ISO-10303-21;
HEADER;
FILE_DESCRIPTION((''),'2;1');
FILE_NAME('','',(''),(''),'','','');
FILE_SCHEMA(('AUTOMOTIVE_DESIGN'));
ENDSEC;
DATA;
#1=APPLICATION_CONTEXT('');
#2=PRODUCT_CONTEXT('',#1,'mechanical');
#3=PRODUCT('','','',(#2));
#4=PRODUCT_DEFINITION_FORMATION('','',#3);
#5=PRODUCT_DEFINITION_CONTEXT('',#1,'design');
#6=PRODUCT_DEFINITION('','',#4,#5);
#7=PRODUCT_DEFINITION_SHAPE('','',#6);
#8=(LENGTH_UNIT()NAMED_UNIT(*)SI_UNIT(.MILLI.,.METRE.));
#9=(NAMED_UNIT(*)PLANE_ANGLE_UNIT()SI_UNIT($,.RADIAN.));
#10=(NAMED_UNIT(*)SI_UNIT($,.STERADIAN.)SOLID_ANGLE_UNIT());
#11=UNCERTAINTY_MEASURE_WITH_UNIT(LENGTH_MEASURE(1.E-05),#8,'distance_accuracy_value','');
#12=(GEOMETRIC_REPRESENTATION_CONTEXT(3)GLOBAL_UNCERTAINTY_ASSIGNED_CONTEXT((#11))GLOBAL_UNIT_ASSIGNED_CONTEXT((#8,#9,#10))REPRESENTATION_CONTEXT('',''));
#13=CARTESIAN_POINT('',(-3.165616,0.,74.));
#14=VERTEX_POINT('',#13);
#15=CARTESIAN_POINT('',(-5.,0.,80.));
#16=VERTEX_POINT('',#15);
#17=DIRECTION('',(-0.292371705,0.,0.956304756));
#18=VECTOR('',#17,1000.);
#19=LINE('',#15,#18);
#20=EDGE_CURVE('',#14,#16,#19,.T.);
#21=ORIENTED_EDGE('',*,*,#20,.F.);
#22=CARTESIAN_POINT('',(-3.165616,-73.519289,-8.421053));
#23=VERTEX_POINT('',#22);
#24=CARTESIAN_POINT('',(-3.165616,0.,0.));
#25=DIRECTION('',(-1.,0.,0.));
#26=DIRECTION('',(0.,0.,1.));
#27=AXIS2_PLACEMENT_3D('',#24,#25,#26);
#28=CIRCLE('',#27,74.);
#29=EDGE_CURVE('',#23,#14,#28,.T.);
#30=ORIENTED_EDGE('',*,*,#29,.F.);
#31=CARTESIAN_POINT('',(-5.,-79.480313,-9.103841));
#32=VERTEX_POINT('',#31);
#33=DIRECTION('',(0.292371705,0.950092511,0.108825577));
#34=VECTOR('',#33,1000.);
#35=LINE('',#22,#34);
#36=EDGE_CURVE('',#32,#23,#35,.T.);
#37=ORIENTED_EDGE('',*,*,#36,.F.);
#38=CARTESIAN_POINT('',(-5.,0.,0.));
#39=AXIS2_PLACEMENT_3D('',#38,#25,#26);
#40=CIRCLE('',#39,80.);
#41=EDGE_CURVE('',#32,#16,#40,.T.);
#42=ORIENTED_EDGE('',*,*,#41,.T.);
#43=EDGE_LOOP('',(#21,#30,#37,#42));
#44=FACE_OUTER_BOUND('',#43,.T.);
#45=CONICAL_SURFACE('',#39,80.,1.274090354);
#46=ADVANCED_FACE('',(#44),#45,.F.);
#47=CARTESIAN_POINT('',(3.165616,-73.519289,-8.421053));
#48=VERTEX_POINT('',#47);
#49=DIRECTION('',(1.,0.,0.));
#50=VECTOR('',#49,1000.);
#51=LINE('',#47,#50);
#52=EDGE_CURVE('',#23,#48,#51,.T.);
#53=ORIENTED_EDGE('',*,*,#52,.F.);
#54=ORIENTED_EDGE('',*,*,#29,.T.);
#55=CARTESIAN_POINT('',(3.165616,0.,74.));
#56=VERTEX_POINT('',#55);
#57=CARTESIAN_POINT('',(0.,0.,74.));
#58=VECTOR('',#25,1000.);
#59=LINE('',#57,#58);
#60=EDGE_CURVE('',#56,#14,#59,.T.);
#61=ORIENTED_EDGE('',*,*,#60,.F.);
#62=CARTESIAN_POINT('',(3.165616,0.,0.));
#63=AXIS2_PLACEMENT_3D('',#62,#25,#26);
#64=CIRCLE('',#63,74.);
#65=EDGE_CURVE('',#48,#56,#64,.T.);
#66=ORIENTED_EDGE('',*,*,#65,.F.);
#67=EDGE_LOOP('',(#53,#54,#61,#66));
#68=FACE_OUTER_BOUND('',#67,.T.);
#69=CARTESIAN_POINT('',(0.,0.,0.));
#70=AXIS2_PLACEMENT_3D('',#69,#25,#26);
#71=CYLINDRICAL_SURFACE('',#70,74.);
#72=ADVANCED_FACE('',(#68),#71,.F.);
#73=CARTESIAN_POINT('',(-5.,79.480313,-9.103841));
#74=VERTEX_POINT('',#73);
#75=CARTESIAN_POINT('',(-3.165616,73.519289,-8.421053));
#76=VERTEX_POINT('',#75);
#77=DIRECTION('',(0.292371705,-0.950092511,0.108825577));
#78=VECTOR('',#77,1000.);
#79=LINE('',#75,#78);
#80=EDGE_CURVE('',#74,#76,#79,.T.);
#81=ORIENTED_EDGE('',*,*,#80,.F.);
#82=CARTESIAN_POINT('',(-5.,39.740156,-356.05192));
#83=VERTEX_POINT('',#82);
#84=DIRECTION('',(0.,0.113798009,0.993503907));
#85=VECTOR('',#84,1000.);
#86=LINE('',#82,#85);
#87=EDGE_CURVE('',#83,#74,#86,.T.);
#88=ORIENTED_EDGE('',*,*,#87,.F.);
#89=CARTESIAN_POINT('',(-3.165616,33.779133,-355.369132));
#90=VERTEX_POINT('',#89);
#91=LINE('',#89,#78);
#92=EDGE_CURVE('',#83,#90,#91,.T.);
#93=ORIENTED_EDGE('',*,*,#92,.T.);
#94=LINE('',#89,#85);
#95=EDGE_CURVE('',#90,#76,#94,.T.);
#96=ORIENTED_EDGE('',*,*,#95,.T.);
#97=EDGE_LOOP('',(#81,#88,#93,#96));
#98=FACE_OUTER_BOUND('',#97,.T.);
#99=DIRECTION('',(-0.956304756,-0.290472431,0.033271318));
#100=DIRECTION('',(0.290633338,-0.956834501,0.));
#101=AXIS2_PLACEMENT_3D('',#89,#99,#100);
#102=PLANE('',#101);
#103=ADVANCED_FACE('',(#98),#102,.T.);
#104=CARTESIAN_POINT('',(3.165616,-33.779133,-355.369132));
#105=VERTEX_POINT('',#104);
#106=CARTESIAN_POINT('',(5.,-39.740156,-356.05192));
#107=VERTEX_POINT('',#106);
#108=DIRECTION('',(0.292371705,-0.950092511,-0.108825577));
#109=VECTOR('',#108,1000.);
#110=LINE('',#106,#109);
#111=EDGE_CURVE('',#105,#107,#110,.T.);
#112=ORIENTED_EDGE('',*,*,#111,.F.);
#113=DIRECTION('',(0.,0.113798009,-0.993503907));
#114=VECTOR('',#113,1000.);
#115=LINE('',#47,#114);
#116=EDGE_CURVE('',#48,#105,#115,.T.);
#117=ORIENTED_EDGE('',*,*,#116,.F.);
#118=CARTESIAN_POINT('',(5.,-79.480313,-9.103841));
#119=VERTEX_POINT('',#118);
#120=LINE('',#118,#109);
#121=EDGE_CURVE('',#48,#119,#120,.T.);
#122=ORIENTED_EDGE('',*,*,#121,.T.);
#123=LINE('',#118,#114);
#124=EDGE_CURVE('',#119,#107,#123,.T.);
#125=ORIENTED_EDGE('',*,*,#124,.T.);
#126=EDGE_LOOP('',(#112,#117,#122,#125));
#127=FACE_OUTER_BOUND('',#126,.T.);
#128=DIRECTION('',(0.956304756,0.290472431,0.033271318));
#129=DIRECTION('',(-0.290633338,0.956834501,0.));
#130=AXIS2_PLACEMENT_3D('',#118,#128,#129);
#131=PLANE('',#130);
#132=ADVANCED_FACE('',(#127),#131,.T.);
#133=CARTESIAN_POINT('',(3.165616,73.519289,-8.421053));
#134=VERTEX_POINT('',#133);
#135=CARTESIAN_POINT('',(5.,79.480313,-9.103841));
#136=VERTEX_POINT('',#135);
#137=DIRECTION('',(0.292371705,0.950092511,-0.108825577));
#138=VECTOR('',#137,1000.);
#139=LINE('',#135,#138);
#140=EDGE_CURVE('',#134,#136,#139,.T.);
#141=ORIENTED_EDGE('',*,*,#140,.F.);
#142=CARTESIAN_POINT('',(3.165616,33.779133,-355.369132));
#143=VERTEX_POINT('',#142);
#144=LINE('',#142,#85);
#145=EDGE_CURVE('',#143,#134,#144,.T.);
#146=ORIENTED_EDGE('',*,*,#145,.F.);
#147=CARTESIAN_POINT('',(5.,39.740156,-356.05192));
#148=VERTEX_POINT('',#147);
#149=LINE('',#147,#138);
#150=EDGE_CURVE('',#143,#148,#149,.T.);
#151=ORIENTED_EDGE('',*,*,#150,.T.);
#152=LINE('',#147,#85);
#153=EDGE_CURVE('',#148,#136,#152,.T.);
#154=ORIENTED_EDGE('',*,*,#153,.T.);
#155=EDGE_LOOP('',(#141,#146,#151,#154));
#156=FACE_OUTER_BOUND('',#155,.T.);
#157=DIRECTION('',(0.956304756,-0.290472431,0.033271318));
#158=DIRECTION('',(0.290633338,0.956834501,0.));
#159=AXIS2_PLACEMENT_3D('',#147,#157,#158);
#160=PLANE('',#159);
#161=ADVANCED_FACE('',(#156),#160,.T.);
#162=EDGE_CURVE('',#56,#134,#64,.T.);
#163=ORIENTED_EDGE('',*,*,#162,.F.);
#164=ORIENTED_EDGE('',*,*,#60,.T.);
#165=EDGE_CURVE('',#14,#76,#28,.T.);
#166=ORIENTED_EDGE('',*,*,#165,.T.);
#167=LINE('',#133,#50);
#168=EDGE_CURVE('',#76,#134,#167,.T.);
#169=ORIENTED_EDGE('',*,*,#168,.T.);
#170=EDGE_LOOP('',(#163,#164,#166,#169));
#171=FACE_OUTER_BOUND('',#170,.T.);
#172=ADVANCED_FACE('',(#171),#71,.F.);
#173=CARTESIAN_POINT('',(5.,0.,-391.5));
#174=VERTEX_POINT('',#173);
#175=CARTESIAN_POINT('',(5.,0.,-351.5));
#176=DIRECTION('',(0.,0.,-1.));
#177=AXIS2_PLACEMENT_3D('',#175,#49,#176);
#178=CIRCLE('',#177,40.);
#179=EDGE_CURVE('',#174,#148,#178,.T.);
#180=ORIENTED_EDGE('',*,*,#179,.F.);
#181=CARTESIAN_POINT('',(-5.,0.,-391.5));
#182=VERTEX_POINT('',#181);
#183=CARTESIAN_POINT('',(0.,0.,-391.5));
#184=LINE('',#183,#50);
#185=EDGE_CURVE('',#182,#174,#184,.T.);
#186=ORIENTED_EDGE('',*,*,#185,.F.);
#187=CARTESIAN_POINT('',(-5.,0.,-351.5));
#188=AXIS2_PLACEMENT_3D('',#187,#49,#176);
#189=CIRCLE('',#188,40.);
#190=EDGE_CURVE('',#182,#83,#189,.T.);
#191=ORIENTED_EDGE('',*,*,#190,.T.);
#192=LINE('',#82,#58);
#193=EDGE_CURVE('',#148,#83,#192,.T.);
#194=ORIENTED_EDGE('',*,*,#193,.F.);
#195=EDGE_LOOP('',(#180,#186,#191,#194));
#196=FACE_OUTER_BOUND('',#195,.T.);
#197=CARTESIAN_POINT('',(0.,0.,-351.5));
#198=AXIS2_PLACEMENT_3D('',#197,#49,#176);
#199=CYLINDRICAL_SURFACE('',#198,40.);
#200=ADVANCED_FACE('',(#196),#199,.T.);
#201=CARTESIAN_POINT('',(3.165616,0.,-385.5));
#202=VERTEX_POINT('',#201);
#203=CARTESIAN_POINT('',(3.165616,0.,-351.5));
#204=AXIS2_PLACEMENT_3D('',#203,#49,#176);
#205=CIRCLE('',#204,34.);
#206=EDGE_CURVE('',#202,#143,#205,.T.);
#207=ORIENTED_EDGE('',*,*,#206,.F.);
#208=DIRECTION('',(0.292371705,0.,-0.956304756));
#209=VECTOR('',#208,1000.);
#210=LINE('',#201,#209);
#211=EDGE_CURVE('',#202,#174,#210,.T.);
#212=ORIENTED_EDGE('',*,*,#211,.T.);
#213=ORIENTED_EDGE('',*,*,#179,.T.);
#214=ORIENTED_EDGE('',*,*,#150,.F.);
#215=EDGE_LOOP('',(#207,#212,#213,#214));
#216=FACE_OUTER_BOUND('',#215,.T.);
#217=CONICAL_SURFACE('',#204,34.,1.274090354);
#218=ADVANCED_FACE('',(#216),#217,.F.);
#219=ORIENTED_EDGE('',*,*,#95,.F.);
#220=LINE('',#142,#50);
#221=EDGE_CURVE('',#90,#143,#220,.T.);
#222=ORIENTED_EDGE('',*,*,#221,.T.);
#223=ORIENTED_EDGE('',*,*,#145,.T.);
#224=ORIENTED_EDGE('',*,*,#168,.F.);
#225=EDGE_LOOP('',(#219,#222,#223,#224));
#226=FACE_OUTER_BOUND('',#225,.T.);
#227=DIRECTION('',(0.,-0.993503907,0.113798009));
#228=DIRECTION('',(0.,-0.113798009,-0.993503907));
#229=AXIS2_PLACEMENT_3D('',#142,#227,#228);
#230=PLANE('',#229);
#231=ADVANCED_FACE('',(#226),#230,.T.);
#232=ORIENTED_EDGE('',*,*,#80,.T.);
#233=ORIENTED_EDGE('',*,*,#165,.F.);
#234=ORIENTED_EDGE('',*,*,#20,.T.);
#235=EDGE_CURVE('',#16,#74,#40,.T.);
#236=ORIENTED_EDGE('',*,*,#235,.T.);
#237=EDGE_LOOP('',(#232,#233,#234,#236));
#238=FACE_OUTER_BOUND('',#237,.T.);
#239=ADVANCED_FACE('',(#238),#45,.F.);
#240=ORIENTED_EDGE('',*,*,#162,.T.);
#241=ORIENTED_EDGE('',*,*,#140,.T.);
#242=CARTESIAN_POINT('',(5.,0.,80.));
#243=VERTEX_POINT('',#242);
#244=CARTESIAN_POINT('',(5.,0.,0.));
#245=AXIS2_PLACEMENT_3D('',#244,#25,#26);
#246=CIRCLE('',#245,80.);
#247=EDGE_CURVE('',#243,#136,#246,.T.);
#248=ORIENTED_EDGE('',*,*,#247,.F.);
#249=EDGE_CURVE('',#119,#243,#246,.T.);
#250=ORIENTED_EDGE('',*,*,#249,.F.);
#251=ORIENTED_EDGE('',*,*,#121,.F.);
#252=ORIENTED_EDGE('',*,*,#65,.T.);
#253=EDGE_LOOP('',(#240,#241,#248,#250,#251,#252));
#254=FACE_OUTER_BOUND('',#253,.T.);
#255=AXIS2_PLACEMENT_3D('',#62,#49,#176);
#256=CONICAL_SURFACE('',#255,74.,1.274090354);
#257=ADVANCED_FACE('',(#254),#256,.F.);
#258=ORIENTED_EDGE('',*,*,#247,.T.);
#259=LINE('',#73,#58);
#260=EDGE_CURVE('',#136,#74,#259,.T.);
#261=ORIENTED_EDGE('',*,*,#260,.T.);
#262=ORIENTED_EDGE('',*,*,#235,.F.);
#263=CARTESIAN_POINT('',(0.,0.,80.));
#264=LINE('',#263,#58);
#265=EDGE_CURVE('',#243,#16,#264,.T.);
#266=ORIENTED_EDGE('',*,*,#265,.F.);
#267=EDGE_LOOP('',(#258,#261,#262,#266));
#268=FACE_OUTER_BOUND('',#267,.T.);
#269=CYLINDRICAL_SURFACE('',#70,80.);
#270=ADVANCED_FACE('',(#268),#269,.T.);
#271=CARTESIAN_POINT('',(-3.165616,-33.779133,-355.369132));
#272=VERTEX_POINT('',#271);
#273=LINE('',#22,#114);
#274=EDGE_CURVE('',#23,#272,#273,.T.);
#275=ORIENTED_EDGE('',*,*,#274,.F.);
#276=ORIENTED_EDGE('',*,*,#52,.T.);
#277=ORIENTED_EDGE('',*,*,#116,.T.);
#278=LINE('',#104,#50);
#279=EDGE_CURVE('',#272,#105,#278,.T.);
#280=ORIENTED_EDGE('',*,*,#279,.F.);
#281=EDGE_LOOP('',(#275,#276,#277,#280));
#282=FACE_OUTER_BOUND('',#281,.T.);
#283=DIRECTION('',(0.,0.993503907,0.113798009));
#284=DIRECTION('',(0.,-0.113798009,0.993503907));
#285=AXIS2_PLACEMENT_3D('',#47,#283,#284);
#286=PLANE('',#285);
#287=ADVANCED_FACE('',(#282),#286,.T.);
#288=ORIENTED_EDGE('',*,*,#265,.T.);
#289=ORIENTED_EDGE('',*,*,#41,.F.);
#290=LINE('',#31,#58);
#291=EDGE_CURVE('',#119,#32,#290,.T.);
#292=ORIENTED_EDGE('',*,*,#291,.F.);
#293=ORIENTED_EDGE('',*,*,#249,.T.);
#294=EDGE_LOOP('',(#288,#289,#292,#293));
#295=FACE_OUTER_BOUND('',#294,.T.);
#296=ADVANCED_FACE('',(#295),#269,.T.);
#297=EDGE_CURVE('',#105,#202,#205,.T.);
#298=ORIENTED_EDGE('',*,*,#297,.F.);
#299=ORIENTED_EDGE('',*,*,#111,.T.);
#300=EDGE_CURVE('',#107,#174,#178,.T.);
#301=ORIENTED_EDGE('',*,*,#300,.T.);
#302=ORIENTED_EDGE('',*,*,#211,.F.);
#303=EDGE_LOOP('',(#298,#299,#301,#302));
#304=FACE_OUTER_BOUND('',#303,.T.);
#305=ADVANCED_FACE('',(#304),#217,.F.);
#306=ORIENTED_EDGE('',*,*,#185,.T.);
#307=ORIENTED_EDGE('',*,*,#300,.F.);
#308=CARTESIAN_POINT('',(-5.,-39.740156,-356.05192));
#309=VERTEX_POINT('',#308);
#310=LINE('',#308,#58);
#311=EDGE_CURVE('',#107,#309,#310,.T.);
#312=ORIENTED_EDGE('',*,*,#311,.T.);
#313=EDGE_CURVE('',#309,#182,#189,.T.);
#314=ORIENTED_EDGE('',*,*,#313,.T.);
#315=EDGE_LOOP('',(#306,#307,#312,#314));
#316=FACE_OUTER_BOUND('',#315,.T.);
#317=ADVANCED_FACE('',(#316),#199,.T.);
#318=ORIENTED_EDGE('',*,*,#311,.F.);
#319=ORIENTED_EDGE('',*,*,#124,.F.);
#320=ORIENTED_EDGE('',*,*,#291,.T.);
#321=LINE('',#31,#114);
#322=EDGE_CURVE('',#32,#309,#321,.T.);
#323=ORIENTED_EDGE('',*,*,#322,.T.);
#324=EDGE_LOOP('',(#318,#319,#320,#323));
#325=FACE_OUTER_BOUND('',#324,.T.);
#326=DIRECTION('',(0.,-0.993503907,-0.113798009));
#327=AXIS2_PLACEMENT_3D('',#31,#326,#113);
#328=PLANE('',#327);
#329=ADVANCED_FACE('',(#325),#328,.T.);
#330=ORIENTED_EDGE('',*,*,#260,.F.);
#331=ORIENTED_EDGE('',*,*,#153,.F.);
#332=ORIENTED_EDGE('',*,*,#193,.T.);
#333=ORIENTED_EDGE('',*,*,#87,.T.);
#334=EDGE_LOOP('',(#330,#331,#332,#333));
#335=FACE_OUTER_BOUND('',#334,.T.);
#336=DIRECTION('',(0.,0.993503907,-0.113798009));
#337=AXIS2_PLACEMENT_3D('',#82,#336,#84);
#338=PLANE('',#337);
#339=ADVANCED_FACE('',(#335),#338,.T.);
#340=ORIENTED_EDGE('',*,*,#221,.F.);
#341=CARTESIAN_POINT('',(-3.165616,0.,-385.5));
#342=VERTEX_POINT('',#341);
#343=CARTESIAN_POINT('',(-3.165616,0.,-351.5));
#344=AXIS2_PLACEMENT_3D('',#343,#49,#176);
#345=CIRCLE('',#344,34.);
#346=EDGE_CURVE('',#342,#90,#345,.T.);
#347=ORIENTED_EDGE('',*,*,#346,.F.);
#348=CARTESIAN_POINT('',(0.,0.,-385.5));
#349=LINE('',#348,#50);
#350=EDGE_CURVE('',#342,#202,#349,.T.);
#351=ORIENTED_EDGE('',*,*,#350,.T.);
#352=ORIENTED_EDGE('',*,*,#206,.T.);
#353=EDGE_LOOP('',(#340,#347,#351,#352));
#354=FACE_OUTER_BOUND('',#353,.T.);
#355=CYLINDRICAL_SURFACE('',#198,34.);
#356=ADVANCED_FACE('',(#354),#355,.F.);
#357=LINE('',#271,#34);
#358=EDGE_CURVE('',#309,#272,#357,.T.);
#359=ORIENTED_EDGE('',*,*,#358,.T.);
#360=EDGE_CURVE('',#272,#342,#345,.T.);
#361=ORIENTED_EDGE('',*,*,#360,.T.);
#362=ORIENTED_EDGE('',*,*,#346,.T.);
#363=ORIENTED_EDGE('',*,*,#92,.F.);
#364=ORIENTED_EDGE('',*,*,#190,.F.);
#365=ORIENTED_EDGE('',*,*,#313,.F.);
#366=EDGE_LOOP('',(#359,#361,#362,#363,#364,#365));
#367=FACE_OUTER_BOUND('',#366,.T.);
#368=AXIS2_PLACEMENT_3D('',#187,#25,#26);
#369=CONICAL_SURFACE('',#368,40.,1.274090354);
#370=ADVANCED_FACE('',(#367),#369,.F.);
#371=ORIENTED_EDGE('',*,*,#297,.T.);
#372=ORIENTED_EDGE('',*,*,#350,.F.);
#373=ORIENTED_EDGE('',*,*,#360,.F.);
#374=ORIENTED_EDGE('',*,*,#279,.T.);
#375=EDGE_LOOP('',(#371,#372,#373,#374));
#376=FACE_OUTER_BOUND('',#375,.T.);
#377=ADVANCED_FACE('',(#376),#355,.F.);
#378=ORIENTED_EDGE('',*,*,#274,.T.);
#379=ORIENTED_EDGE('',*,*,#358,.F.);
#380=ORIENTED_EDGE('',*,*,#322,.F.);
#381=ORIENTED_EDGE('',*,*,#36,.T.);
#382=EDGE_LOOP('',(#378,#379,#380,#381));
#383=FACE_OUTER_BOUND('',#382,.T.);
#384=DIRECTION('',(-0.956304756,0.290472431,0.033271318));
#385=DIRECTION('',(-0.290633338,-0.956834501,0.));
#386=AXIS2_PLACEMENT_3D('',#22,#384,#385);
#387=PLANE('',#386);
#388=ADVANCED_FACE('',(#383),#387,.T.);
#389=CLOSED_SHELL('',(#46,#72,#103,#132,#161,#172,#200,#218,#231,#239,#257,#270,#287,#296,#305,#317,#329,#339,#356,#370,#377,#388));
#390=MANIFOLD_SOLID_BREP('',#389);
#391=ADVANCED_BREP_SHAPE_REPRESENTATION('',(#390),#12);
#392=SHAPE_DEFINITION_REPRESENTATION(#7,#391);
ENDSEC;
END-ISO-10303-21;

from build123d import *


with BuildPart() as part:
    # 扫描1: sweep along a path in 草图1
    with BuildLine(Plane(origin=(0, 0, 0), x_dir=(0, 0, -1), z_dir=(1, 0, 0))) as sweep_1_path:
        Line((9.103840683, 79.480312561), (356.051920341, 39.740156281))
        ThreePointArc((356.051920341, 39.740156281), (391.5, 0), (356.051920341, -39.740156281))
        Line((356.051920341, -39.740156281), (9.103840683, -79.480312561))
        ThreePointArc((9.103840683, -79.480312561), (-80, 0), (9.103840683, 79.480312561))
    # 草图2 → 扫描1 (sweep)
    with BuildSketch(Plane.XY):
        Polygon((-5, 80), (5, 80), (3.165615911, 74), (-3.165615911, 74), align=None)
    sweep(path=sweep_1_path.line)


solid = part.part
